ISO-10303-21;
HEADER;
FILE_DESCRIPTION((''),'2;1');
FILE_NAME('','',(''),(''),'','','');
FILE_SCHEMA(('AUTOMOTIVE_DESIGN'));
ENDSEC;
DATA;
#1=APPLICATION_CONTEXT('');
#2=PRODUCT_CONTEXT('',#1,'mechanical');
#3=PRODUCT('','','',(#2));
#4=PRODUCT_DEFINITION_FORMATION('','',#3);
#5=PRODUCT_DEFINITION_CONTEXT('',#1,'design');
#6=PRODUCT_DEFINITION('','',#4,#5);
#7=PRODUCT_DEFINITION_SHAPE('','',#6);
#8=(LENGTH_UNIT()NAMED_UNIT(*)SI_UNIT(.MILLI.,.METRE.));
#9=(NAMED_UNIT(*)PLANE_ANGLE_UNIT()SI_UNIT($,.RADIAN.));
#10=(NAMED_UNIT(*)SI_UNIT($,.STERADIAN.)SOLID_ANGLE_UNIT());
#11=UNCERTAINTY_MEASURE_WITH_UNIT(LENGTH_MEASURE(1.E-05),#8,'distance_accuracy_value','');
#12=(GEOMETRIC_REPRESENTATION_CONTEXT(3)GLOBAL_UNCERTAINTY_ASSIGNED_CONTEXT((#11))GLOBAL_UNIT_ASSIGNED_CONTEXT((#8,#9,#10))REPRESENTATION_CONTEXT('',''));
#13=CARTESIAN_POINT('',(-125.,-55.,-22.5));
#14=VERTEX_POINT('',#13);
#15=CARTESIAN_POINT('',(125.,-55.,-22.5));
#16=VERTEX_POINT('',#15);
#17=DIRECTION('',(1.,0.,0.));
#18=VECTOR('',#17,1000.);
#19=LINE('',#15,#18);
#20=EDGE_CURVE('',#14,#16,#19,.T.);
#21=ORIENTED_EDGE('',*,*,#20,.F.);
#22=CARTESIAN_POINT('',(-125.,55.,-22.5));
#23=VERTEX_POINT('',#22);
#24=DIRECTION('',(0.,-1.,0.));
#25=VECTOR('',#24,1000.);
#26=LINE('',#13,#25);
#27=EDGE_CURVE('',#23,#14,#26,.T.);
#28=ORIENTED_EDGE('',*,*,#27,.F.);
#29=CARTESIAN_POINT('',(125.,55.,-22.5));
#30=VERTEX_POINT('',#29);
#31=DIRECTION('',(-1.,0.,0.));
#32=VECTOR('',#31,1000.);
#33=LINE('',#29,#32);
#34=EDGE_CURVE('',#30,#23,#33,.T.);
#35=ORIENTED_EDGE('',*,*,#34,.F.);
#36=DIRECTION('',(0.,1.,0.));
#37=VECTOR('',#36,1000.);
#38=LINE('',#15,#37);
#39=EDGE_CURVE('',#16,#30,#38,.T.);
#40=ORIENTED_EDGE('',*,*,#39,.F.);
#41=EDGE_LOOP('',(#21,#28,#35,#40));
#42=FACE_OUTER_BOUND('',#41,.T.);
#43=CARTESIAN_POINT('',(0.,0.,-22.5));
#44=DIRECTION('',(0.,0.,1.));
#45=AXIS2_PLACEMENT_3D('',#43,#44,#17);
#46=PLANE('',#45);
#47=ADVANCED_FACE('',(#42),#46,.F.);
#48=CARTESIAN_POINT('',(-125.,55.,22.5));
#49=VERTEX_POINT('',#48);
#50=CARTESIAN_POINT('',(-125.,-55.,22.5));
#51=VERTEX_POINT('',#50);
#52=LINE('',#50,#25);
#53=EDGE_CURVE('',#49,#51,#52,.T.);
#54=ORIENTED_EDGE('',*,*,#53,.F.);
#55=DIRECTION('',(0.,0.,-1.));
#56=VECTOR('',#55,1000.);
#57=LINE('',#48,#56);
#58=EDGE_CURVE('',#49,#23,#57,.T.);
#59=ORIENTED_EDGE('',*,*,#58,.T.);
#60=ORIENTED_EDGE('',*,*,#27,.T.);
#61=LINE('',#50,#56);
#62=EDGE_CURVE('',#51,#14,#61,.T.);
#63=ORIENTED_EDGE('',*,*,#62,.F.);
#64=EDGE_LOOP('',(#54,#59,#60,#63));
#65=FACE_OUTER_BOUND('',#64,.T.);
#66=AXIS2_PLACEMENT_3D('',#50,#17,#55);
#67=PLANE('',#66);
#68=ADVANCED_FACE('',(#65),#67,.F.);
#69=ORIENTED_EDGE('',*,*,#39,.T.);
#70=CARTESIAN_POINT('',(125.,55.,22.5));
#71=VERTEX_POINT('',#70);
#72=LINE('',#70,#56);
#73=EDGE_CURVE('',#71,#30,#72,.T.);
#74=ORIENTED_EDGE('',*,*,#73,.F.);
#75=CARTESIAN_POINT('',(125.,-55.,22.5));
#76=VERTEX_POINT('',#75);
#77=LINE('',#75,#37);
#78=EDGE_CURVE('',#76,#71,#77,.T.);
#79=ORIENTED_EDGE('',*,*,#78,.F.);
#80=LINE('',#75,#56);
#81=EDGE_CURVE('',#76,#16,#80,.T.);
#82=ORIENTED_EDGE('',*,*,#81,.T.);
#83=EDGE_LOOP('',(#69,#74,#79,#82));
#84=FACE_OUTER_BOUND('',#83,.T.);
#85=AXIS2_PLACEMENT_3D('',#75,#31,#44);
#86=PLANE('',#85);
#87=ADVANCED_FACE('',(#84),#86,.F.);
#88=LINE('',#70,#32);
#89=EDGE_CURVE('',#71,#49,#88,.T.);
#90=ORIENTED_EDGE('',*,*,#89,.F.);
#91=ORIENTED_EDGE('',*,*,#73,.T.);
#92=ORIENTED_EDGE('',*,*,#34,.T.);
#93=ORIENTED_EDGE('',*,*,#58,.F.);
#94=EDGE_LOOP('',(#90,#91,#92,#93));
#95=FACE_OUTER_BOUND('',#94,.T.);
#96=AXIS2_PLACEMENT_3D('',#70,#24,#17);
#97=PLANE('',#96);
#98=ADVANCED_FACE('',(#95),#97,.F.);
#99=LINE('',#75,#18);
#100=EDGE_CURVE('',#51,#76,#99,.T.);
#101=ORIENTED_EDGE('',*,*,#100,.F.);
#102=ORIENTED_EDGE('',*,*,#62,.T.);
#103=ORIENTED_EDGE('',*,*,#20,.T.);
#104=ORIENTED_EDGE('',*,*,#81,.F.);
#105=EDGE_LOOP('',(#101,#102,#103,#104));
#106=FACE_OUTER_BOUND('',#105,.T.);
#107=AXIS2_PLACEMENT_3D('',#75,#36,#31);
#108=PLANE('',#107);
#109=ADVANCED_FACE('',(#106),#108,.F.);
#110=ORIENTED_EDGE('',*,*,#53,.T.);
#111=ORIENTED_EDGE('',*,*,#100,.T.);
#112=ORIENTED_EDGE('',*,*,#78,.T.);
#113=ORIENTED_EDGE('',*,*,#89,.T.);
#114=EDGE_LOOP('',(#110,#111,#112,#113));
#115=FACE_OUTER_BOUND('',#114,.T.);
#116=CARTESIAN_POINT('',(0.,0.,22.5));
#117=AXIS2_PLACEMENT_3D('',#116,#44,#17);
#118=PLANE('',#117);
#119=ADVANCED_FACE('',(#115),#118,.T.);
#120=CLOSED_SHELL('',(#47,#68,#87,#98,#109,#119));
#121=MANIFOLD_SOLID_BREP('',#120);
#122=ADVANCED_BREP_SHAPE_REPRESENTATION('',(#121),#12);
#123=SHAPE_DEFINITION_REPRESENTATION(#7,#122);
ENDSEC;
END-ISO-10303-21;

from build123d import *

# Parameters (mm, degrees)
SKETCH1_W           = 250
SKETCH1_H           = 110
BOSS_EXTRUDE1_DEPTH = 22.5


with BuildPart() as part:
    # Sketch1 → Boss-Extrude1 (new, symmetric)
    with BuildSketch(Plane.XY):
        Rectangle(SKETCH1_W, SKETCH1_H)
    extrude(amount=BOSS_EXTRUDE1_DEPTH, both=True)


solid = part.part
